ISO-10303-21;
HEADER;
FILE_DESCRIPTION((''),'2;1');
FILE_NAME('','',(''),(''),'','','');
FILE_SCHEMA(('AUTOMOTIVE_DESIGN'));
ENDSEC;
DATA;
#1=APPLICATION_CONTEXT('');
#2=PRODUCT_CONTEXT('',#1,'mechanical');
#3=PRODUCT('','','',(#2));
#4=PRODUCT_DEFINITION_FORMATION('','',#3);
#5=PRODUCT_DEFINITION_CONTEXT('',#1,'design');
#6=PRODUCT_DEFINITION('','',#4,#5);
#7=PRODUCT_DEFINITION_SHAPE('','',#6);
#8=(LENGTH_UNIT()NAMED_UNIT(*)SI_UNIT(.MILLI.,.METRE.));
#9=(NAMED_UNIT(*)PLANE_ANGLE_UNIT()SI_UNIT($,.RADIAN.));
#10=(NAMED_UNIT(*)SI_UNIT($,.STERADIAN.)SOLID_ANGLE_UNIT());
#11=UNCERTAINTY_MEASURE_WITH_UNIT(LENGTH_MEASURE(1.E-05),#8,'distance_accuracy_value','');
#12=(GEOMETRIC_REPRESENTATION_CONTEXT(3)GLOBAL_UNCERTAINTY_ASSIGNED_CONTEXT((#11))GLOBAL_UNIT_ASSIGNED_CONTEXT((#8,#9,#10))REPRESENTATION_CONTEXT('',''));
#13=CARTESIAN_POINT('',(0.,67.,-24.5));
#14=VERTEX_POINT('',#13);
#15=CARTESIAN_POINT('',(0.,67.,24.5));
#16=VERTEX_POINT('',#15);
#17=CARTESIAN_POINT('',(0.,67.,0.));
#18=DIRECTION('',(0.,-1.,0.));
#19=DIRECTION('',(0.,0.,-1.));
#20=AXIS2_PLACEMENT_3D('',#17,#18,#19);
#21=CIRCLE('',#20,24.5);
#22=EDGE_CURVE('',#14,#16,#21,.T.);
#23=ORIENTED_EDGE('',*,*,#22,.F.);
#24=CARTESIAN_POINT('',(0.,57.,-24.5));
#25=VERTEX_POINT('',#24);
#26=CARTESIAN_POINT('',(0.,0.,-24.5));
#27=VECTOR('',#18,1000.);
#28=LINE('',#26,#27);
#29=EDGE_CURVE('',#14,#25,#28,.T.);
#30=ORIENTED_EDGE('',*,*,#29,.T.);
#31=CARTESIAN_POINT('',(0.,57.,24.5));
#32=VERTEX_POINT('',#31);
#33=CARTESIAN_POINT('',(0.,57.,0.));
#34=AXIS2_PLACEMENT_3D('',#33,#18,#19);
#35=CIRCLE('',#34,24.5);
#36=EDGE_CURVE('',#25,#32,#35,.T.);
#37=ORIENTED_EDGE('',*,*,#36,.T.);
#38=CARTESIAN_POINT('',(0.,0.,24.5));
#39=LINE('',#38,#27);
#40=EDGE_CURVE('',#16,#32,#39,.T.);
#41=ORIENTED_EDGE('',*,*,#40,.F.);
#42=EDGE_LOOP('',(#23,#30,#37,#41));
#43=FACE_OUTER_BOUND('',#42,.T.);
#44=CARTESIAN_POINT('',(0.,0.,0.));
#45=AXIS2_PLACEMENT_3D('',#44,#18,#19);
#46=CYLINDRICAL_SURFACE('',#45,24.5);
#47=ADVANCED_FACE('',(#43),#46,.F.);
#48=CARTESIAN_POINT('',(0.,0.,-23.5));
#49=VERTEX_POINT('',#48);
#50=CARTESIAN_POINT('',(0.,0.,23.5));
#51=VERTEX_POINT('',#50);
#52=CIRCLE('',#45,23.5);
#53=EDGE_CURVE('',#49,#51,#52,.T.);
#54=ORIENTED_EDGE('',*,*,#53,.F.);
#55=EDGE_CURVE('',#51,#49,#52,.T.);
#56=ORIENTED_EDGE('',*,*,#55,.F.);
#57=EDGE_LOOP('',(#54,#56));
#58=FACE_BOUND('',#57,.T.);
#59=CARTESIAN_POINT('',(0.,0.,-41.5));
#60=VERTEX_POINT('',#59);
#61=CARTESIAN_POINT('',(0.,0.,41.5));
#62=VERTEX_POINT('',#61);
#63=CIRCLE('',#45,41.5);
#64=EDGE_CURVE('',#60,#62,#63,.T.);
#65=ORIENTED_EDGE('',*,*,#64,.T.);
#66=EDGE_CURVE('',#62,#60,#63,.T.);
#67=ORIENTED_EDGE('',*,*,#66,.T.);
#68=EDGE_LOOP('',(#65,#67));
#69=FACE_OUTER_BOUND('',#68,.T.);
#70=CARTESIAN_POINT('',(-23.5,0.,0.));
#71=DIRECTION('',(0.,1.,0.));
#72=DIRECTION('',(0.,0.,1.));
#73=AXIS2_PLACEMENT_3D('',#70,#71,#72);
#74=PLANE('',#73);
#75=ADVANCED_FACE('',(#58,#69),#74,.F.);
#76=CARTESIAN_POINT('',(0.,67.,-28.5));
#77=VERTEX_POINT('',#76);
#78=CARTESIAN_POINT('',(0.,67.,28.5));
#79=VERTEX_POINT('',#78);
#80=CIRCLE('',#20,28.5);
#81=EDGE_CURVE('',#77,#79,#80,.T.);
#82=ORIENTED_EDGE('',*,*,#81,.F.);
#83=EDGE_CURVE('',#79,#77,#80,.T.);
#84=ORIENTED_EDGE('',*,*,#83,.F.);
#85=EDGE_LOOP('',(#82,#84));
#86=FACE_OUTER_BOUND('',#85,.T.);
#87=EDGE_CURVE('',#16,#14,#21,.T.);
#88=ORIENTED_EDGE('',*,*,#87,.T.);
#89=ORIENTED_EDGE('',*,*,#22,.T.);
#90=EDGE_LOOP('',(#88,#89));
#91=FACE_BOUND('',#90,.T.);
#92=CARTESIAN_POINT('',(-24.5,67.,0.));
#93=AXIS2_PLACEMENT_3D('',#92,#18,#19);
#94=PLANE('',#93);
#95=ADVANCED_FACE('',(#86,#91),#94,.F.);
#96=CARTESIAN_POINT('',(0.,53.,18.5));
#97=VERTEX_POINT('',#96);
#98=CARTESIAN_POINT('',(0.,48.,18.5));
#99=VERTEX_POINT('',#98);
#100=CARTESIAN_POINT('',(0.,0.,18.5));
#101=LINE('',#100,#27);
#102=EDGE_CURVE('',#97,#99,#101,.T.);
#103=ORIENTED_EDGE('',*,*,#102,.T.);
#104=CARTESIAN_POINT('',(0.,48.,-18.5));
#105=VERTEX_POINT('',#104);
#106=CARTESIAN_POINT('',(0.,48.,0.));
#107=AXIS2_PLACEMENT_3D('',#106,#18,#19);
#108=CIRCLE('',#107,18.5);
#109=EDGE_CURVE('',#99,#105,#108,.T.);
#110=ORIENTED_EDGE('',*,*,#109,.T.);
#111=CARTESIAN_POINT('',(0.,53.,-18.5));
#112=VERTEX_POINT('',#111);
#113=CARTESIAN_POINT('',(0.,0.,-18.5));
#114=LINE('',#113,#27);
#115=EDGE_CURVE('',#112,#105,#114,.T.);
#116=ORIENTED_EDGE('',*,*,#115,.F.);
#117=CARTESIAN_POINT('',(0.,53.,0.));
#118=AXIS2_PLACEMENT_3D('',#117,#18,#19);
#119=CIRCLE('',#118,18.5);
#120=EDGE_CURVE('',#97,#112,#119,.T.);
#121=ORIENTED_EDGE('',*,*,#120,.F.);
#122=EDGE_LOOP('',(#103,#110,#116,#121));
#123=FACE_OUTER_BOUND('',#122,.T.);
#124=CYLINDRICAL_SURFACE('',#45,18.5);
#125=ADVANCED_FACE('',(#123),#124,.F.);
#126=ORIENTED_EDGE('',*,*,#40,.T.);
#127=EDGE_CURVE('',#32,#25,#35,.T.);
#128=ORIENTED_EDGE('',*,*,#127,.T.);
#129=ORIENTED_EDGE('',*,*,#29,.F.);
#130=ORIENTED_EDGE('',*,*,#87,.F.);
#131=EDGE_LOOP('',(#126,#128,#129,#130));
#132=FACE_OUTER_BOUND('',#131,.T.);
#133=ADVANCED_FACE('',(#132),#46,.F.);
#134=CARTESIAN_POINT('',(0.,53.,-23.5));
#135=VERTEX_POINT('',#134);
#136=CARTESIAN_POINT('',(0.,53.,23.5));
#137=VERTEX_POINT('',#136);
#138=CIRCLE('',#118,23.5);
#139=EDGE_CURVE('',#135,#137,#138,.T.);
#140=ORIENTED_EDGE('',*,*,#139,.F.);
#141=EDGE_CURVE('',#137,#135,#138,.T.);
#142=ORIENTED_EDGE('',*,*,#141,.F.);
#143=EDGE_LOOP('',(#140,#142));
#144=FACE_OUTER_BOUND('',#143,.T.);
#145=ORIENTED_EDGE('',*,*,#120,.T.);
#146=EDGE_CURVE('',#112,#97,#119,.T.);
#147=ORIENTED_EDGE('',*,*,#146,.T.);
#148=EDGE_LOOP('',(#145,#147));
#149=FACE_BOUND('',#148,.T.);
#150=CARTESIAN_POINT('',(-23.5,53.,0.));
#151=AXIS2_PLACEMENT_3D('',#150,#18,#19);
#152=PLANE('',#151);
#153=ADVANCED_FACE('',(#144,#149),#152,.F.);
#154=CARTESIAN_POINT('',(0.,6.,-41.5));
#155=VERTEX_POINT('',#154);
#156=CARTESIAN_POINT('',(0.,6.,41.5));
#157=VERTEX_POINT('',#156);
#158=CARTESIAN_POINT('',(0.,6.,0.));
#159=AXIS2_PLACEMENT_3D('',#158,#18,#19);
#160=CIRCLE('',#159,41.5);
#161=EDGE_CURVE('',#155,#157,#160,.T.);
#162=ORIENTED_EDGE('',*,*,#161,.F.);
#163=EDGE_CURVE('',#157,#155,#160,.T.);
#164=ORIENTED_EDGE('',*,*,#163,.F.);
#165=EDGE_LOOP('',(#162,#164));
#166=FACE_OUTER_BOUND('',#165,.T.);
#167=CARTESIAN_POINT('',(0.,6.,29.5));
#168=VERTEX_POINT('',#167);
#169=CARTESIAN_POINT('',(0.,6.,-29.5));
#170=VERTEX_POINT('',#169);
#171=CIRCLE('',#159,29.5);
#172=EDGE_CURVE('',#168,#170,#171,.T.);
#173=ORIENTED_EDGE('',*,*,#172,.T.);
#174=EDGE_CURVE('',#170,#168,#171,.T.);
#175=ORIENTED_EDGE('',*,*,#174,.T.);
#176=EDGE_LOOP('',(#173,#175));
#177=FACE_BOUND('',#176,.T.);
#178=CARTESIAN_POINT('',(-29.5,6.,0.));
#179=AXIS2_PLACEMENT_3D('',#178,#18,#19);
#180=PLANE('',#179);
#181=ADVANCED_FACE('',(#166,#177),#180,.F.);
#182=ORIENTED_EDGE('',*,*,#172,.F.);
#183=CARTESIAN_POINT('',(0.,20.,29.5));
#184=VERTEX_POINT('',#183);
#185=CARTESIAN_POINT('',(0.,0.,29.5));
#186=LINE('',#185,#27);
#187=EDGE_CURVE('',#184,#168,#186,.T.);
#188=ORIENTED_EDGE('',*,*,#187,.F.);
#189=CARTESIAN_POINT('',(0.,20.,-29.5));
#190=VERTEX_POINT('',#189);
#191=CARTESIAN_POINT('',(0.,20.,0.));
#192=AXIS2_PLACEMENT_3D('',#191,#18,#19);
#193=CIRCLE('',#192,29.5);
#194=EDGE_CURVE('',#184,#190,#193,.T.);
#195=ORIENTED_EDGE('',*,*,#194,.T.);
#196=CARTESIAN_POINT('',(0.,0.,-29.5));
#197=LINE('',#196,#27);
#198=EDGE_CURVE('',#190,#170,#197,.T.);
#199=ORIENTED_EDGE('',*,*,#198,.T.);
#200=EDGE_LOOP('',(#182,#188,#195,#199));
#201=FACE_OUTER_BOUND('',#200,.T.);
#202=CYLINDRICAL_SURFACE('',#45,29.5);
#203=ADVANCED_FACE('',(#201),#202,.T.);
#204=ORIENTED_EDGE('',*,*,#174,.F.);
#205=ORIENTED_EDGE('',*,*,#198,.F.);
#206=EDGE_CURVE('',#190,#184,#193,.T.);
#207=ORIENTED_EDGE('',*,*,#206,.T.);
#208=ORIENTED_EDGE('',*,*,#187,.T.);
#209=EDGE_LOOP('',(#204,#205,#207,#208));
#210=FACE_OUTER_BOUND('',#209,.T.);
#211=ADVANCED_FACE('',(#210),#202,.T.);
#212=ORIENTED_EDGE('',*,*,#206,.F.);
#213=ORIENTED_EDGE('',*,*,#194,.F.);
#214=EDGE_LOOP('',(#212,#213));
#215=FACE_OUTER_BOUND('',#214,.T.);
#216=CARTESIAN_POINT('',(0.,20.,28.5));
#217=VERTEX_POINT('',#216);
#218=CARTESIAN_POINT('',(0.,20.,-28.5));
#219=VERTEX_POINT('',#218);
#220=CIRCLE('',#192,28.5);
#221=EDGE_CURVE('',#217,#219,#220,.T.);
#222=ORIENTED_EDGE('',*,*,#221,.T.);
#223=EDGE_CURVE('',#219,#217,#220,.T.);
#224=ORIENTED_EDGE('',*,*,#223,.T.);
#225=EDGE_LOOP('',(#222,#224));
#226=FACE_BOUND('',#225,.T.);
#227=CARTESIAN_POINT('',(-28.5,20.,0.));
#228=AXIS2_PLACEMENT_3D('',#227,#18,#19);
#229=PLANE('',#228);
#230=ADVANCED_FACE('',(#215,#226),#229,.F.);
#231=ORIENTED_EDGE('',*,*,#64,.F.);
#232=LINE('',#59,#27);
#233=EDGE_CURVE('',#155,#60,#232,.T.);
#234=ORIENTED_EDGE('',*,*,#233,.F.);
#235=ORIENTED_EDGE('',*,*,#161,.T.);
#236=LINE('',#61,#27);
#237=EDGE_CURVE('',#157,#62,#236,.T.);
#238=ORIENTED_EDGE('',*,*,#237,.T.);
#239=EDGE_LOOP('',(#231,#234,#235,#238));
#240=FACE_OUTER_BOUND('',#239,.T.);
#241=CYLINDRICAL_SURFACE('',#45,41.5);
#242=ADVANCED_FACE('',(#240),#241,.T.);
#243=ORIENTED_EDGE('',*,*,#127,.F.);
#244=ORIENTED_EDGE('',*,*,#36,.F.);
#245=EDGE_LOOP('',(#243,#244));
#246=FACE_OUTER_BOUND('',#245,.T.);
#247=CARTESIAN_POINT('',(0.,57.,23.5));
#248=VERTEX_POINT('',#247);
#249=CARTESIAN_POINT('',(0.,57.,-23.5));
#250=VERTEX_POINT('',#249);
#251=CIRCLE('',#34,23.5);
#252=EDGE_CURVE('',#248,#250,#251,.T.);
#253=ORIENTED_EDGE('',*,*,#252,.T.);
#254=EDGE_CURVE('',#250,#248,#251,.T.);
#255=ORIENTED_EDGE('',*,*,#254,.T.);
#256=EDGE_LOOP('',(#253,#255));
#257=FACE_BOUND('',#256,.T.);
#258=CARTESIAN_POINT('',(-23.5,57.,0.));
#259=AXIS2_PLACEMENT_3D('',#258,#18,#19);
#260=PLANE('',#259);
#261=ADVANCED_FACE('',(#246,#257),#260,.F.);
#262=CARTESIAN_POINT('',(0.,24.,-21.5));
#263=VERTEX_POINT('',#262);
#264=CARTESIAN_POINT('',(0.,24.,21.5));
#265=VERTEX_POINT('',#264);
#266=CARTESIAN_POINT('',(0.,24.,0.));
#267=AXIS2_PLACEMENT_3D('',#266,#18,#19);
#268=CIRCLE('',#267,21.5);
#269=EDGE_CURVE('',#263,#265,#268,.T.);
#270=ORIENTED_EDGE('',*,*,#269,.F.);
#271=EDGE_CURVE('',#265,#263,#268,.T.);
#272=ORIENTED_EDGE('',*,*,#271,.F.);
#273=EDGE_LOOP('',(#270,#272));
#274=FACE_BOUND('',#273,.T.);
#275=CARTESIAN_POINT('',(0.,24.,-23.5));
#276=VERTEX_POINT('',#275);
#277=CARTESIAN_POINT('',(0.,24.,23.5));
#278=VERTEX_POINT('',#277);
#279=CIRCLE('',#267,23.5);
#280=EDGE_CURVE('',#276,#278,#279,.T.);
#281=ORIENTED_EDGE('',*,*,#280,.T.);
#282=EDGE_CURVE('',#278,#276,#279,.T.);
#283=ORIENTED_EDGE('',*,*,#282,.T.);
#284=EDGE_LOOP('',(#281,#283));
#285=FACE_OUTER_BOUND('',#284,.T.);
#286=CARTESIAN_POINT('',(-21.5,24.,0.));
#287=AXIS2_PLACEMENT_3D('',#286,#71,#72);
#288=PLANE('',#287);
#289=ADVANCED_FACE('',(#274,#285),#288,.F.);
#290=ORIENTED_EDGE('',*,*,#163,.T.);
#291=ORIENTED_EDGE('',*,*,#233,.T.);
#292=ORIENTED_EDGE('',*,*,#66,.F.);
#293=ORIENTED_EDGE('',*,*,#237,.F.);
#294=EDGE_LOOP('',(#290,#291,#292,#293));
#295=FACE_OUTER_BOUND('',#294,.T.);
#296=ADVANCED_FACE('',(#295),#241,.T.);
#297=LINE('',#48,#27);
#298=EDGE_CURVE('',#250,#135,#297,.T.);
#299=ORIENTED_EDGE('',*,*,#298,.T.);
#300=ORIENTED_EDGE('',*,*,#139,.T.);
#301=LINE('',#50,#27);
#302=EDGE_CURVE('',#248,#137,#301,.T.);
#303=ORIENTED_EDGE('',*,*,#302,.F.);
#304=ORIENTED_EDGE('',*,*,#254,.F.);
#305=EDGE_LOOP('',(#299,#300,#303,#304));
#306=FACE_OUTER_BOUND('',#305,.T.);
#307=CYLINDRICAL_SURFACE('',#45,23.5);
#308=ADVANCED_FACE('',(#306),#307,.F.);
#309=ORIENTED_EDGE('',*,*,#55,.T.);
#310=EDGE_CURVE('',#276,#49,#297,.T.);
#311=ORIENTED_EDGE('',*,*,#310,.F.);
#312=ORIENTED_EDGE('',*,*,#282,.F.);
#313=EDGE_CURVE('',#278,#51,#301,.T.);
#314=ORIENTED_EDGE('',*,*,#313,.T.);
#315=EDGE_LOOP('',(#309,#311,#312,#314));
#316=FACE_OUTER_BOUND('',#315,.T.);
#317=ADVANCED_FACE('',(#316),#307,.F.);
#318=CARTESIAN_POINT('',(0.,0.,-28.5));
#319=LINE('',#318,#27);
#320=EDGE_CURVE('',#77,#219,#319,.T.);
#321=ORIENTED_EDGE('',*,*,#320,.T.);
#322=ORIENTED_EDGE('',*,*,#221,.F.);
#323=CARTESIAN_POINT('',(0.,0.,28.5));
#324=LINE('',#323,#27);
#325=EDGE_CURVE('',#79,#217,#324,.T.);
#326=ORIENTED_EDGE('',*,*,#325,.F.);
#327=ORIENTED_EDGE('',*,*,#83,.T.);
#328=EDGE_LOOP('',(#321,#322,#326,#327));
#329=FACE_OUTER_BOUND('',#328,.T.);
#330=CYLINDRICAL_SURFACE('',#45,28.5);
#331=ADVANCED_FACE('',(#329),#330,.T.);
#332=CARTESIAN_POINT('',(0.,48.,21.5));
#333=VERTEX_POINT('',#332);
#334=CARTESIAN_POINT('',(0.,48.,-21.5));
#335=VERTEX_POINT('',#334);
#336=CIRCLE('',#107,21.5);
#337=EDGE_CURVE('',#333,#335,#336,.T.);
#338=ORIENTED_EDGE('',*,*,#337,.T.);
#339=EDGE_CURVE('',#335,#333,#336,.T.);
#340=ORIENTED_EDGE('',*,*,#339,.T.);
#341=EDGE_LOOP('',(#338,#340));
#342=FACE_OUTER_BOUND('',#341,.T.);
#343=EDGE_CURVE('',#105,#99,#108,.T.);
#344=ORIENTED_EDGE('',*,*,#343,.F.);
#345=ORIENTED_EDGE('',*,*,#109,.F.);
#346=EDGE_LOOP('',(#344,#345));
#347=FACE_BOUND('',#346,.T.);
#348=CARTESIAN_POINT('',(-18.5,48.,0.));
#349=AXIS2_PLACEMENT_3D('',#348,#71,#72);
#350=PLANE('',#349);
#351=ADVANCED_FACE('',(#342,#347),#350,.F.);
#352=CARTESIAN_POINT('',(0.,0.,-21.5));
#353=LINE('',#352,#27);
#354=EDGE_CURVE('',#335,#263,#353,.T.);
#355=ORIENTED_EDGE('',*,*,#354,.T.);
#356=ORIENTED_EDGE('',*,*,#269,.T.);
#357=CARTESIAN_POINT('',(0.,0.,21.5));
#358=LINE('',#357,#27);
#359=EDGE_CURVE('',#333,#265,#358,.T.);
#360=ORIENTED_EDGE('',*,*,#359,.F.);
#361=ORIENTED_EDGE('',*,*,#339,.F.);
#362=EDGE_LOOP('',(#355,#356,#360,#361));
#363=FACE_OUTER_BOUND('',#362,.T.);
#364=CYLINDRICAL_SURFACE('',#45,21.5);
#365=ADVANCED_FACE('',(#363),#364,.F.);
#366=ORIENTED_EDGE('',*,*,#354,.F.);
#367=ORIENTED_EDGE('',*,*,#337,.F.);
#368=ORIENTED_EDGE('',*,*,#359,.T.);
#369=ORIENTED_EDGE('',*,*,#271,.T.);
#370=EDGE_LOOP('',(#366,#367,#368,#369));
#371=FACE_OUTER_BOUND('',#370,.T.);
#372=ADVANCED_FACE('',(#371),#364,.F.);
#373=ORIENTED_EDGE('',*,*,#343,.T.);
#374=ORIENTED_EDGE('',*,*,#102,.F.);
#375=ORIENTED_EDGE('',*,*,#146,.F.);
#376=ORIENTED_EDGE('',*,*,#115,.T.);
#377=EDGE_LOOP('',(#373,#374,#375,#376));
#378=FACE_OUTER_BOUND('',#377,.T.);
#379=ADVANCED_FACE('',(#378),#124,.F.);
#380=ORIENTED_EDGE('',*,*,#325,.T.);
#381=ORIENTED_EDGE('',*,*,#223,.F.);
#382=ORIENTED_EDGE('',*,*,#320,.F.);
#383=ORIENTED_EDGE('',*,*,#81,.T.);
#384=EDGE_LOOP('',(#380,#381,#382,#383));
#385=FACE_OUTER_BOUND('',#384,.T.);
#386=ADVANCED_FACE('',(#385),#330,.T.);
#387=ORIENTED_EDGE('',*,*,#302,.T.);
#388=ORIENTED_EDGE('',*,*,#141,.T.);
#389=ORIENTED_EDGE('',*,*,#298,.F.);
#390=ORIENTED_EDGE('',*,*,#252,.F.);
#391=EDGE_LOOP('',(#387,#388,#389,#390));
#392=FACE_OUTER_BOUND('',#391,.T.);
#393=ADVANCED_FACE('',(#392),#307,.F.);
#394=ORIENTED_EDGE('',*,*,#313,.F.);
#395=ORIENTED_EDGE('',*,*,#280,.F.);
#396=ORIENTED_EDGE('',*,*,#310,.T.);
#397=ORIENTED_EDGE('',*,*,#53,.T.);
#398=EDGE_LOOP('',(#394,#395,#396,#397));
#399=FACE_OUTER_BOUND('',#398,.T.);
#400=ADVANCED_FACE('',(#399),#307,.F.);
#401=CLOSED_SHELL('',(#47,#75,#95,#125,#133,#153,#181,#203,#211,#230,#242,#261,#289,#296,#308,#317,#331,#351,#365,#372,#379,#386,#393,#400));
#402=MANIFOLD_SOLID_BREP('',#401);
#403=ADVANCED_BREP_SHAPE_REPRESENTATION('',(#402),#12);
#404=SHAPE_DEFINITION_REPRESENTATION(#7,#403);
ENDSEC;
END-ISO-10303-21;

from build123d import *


with BuildPart() as part:
    # 草图1 → 旋转1 (revolve)
    with BuildSketch(Plane.XY, mode=Mode.PRIVATE) as revolve_1_sk:
        Polygon((-23.5, 57), (-23.5, 53), (-18.5, 53), (-18.5, 48), (-21.5, 48), (-21.5, 24), (-23.5, 24), (-23.5, 0), (-41.5, 0), (-41.5, 6), (-29.5, 6), (-29.5, 20), (-28.5, 20), (-28.5, 67), (-24.5, 67), (-24.5, 57), align=None)
    revolve(revolve_1_sk.sketch.rotate(Axis((0, 0, 0), (0, 1, 0)), 270), axis=Axis((0, 0, 0), (0, 1, 0)))


solid = part.part
